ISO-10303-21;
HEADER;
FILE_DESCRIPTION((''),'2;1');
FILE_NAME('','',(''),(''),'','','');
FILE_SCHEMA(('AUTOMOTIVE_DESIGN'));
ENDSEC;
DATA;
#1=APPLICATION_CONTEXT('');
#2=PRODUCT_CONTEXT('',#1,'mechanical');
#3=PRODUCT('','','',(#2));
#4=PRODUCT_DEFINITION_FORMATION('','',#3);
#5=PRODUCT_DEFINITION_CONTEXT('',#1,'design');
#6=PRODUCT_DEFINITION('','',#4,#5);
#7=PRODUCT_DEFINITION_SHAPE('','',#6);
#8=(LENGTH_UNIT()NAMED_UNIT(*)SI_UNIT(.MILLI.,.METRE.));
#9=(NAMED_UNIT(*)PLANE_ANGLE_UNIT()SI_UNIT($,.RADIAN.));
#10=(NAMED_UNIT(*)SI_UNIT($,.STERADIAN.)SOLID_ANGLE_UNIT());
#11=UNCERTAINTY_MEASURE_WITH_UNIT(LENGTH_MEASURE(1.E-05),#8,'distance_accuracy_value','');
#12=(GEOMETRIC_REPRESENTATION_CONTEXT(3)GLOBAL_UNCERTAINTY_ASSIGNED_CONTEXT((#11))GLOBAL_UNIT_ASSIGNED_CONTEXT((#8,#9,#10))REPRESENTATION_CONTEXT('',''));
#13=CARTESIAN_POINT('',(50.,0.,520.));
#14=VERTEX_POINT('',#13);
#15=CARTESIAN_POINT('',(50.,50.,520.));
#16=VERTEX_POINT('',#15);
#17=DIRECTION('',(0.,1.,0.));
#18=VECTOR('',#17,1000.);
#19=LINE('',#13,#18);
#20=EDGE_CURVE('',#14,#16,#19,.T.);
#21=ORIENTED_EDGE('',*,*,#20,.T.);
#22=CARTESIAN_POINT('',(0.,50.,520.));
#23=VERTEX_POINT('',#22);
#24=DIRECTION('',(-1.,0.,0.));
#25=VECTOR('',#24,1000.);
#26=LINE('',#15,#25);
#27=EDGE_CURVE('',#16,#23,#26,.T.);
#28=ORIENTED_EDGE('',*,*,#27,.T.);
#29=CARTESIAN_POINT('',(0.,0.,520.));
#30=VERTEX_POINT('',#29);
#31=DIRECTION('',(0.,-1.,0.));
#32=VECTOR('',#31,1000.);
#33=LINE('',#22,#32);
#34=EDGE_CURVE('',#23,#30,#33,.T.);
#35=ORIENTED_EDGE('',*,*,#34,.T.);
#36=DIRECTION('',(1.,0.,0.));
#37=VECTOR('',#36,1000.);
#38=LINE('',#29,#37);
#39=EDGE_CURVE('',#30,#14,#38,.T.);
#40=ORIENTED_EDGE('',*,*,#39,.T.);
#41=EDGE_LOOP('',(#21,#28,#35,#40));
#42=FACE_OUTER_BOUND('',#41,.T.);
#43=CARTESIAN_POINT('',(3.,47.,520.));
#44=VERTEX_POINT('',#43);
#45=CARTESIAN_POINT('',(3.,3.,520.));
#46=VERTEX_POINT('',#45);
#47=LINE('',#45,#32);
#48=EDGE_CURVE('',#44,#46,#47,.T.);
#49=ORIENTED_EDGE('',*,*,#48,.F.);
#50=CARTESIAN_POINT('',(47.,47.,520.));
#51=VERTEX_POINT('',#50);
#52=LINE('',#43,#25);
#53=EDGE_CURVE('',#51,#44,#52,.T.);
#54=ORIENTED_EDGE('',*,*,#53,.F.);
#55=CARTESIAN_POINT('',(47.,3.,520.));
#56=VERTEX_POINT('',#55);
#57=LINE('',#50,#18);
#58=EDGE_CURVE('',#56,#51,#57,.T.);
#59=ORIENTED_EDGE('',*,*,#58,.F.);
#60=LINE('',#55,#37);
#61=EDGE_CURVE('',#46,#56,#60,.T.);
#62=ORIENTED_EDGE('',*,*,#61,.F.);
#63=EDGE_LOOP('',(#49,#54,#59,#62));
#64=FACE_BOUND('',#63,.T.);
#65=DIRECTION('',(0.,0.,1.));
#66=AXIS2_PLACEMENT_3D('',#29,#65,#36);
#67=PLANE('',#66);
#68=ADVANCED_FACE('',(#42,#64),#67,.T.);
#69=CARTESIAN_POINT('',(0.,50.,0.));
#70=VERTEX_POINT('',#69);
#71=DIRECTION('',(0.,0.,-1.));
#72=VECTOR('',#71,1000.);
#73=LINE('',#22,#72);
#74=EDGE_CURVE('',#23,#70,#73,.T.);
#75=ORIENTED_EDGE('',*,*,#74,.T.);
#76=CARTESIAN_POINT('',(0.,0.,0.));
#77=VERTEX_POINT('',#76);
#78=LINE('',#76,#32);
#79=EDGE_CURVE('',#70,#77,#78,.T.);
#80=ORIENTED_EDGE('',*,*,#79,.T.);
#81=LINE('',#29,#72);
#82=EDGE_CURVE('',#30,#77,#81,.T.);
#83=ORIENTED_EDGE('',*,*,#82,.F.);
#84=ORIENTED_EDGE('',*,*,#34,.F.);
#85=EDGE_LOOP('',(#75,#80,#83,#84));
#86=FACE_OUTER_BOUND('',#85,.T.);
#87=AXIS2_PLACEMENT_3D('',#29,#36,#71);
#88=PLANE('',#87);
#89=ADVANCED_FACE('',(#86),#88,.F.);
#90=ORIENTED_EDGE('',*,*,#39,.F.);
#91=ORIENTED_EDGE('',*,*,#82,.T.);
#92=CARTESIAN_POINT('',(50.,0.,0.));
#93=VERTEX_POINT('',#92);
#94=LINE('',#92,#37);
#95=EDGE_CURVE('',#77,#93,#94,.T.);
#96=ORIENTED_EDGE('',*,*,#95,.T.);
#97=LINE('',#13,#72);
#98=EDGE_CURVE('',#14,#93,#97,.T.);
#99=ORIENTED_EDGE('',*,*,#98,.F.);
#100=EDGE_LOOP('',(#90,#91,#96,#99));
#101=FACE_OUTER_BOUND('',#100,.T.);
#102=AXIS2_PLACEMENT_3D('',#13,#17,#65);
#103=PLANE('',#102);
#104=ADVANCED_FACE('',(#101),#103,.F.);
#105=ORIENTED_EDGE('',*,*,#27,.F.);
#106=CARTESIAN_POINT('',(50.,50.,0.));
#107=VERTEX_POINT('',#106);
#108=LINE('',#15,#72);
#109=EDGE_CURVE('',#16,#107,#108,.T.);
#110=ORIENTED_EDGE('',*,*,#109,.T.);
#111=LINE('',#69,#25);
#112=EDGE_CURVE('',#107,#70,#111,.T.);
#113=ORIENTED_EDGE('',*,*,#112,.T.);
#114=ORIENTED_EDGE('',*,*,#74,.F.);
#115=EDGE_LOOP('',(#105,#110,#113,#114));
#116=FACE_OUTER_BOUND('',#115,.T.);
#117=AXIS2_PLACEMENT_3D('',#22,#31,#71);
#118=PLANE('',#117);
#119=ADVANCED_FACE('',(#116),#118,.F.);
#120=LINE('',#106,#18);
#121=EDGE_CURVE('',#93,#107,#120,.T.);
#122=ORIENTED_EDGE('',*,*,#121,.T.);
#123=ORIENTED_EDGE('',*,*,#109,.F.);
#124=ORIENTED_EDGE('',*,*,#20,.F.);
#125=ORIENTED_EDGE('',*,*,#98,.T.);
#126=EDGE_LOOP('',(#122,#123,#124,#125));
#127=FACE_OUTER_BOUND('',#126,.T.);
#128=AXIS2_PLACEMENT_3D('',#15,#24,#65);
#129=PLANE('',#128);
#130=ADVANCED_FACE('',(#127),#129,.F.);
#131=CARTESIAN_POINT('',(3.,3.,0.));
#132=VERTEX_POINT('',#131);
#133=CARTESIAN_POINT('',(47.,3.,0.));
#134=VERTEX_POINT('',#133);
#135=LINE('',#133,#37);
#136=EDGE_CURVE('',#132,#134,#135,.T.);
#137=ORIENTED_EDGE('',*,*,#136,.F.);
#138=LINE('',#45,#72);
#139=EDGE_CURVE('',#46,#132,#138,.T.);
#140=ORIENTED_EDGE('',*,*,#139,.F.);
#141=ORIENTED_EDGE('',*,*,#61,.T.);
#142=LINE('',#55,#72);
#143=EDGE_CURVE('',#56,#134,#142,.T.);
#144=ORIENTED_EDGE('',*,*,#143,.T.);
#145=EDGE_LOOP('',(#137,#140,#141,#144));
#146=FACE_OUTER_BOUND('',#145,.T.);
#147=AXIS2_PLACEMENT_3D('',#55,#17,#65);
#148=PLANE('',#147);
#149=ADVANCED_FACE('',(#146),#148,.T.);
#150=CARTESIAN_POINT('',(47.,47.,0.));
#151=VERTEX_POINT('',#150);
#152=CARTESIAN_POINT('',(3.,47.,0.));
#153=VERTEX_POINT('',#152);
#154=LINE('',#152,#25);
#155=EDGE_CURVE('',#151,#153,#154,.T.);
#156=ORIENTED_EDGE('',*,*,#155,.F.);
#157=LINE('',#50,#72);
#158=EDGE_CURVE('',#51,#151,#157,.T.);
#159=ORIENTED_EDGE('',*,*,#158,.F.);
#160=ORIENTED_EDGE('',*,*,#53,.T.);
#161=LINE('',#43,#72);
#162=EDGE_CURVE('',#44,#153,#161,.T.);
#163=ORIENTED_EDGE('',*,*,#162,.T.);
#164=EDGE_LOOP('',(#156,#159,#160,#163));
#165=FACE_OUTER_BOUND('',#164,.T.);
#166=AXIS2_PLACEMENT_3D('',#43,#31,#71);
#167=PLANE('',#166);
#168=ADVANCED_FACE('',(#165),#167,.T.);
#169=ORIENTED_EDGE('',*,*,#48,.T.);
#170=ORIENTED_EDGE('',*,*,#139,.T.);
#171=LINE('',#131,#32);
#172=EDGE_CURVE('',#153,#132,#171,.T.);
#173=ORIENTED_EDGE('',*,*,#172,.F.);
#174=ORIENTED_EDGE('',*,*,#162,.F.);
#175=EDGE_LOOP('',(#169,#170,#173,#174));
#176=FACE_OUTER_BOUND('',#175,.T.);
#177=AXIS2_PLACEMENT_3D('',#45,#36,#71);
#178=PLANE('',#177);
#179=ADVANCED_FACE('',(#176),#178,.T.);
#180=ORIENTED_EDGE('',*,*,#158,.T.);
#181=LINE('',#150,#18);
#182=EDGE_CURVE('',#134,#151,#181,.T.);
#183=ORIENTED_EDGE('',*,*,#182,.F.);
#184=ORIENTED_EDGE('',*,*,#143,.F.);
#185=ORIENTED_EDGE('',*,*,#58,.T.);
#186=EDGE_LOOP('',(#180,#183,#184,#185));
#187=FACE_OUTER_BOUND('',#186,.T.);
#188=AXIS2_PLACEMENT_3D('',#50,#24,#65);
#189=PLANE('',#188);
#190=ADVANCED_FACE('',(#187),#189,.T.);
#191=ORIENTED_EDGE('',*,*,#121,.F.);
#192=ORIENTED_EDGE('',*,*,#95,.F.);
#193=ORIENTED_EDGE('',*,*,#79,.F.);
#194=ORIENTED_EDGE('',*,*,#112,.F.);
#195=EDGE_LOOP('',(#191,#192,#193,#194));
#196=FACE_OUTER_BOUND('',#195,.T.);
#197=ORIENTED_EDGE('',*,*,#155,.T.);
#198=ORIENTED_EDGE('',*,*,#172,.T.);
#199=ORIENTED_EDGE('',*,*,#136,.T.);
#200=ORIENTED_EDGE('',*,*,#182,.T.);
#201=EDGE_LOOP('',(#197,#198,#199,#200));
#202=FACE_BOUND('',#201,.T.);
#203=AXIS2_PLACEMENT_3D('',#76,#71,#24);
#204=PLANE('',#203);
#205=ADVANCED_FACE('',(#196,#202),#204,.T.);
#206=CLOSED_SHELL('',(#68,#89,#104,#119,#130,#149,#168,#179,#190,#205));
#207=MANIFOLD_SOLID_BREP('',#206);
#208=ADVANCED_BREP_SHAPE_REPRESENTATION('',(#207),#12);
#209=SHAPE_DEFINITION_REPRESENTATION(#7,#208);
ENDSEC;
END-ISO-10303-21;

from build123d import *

# Parameters (mm, degrees)
SKETCH_1_W          = 50
SKETCH_1_H          = 50
SKETCH_1_W_2        = 44
SKETCH_1_H_2        = 44
EXTRUDE_1_DEPTH     = 520
SKETCH_2_W          = 56
SKETCH_2_H          = 56
CUT_EXTRUDE_1_DEPTH = 100
SKETCH_3_W          = 50
SKETCH_3_H          = 50
SKETCH_3_W_2        = 44
SKETCH_3_H_2        = 44
EXTRUDE_2_DEPTH     = 100


with BuildPart() as part:
    # 草图1 → 凸台-拉伸1 (new body)
    with BuildSketch(Plane.XY):
        with Locations((25, 25)):
            Rectangle(SKETCH_1_W, SKETCH_1_H)
        with Locations((25, 25)):
            Rectangle(SKETCH_1_W_2, SKETCH_1_H_2, mode=Mode.SUBTRACT)
    extrude(amount=EXTRUDE_1_DEPTH)

    # 草图2 → 切除-拉伸1 (cut)
    with BuildSketch(Plane.XY.offset(520)):
        with Locations((25, 25)):
            Rectangle(SKETCH_2_W, SKETCH_2_H)
    extrude(amount=-CUT_EXTRUDE_1_DEPTH, mode=Mode.SUBTRACT)

    # 草图3 → 凸台-拉伸2 (add)
    with BuildSketch(Plane.XY.offset(420)):
        with Locations((25, 25)):
            Rectangle(SKETCH_3_W, SKETCH_3_H)
        with Locations((25, 25)):
            Rectangle(SKETCH_3_W_2, SKETCH_3_H_2, mode=Mode.SUBTRACT)
    extrude(amount=EXTRUDE_2_DEPTH)


solid = part.part
